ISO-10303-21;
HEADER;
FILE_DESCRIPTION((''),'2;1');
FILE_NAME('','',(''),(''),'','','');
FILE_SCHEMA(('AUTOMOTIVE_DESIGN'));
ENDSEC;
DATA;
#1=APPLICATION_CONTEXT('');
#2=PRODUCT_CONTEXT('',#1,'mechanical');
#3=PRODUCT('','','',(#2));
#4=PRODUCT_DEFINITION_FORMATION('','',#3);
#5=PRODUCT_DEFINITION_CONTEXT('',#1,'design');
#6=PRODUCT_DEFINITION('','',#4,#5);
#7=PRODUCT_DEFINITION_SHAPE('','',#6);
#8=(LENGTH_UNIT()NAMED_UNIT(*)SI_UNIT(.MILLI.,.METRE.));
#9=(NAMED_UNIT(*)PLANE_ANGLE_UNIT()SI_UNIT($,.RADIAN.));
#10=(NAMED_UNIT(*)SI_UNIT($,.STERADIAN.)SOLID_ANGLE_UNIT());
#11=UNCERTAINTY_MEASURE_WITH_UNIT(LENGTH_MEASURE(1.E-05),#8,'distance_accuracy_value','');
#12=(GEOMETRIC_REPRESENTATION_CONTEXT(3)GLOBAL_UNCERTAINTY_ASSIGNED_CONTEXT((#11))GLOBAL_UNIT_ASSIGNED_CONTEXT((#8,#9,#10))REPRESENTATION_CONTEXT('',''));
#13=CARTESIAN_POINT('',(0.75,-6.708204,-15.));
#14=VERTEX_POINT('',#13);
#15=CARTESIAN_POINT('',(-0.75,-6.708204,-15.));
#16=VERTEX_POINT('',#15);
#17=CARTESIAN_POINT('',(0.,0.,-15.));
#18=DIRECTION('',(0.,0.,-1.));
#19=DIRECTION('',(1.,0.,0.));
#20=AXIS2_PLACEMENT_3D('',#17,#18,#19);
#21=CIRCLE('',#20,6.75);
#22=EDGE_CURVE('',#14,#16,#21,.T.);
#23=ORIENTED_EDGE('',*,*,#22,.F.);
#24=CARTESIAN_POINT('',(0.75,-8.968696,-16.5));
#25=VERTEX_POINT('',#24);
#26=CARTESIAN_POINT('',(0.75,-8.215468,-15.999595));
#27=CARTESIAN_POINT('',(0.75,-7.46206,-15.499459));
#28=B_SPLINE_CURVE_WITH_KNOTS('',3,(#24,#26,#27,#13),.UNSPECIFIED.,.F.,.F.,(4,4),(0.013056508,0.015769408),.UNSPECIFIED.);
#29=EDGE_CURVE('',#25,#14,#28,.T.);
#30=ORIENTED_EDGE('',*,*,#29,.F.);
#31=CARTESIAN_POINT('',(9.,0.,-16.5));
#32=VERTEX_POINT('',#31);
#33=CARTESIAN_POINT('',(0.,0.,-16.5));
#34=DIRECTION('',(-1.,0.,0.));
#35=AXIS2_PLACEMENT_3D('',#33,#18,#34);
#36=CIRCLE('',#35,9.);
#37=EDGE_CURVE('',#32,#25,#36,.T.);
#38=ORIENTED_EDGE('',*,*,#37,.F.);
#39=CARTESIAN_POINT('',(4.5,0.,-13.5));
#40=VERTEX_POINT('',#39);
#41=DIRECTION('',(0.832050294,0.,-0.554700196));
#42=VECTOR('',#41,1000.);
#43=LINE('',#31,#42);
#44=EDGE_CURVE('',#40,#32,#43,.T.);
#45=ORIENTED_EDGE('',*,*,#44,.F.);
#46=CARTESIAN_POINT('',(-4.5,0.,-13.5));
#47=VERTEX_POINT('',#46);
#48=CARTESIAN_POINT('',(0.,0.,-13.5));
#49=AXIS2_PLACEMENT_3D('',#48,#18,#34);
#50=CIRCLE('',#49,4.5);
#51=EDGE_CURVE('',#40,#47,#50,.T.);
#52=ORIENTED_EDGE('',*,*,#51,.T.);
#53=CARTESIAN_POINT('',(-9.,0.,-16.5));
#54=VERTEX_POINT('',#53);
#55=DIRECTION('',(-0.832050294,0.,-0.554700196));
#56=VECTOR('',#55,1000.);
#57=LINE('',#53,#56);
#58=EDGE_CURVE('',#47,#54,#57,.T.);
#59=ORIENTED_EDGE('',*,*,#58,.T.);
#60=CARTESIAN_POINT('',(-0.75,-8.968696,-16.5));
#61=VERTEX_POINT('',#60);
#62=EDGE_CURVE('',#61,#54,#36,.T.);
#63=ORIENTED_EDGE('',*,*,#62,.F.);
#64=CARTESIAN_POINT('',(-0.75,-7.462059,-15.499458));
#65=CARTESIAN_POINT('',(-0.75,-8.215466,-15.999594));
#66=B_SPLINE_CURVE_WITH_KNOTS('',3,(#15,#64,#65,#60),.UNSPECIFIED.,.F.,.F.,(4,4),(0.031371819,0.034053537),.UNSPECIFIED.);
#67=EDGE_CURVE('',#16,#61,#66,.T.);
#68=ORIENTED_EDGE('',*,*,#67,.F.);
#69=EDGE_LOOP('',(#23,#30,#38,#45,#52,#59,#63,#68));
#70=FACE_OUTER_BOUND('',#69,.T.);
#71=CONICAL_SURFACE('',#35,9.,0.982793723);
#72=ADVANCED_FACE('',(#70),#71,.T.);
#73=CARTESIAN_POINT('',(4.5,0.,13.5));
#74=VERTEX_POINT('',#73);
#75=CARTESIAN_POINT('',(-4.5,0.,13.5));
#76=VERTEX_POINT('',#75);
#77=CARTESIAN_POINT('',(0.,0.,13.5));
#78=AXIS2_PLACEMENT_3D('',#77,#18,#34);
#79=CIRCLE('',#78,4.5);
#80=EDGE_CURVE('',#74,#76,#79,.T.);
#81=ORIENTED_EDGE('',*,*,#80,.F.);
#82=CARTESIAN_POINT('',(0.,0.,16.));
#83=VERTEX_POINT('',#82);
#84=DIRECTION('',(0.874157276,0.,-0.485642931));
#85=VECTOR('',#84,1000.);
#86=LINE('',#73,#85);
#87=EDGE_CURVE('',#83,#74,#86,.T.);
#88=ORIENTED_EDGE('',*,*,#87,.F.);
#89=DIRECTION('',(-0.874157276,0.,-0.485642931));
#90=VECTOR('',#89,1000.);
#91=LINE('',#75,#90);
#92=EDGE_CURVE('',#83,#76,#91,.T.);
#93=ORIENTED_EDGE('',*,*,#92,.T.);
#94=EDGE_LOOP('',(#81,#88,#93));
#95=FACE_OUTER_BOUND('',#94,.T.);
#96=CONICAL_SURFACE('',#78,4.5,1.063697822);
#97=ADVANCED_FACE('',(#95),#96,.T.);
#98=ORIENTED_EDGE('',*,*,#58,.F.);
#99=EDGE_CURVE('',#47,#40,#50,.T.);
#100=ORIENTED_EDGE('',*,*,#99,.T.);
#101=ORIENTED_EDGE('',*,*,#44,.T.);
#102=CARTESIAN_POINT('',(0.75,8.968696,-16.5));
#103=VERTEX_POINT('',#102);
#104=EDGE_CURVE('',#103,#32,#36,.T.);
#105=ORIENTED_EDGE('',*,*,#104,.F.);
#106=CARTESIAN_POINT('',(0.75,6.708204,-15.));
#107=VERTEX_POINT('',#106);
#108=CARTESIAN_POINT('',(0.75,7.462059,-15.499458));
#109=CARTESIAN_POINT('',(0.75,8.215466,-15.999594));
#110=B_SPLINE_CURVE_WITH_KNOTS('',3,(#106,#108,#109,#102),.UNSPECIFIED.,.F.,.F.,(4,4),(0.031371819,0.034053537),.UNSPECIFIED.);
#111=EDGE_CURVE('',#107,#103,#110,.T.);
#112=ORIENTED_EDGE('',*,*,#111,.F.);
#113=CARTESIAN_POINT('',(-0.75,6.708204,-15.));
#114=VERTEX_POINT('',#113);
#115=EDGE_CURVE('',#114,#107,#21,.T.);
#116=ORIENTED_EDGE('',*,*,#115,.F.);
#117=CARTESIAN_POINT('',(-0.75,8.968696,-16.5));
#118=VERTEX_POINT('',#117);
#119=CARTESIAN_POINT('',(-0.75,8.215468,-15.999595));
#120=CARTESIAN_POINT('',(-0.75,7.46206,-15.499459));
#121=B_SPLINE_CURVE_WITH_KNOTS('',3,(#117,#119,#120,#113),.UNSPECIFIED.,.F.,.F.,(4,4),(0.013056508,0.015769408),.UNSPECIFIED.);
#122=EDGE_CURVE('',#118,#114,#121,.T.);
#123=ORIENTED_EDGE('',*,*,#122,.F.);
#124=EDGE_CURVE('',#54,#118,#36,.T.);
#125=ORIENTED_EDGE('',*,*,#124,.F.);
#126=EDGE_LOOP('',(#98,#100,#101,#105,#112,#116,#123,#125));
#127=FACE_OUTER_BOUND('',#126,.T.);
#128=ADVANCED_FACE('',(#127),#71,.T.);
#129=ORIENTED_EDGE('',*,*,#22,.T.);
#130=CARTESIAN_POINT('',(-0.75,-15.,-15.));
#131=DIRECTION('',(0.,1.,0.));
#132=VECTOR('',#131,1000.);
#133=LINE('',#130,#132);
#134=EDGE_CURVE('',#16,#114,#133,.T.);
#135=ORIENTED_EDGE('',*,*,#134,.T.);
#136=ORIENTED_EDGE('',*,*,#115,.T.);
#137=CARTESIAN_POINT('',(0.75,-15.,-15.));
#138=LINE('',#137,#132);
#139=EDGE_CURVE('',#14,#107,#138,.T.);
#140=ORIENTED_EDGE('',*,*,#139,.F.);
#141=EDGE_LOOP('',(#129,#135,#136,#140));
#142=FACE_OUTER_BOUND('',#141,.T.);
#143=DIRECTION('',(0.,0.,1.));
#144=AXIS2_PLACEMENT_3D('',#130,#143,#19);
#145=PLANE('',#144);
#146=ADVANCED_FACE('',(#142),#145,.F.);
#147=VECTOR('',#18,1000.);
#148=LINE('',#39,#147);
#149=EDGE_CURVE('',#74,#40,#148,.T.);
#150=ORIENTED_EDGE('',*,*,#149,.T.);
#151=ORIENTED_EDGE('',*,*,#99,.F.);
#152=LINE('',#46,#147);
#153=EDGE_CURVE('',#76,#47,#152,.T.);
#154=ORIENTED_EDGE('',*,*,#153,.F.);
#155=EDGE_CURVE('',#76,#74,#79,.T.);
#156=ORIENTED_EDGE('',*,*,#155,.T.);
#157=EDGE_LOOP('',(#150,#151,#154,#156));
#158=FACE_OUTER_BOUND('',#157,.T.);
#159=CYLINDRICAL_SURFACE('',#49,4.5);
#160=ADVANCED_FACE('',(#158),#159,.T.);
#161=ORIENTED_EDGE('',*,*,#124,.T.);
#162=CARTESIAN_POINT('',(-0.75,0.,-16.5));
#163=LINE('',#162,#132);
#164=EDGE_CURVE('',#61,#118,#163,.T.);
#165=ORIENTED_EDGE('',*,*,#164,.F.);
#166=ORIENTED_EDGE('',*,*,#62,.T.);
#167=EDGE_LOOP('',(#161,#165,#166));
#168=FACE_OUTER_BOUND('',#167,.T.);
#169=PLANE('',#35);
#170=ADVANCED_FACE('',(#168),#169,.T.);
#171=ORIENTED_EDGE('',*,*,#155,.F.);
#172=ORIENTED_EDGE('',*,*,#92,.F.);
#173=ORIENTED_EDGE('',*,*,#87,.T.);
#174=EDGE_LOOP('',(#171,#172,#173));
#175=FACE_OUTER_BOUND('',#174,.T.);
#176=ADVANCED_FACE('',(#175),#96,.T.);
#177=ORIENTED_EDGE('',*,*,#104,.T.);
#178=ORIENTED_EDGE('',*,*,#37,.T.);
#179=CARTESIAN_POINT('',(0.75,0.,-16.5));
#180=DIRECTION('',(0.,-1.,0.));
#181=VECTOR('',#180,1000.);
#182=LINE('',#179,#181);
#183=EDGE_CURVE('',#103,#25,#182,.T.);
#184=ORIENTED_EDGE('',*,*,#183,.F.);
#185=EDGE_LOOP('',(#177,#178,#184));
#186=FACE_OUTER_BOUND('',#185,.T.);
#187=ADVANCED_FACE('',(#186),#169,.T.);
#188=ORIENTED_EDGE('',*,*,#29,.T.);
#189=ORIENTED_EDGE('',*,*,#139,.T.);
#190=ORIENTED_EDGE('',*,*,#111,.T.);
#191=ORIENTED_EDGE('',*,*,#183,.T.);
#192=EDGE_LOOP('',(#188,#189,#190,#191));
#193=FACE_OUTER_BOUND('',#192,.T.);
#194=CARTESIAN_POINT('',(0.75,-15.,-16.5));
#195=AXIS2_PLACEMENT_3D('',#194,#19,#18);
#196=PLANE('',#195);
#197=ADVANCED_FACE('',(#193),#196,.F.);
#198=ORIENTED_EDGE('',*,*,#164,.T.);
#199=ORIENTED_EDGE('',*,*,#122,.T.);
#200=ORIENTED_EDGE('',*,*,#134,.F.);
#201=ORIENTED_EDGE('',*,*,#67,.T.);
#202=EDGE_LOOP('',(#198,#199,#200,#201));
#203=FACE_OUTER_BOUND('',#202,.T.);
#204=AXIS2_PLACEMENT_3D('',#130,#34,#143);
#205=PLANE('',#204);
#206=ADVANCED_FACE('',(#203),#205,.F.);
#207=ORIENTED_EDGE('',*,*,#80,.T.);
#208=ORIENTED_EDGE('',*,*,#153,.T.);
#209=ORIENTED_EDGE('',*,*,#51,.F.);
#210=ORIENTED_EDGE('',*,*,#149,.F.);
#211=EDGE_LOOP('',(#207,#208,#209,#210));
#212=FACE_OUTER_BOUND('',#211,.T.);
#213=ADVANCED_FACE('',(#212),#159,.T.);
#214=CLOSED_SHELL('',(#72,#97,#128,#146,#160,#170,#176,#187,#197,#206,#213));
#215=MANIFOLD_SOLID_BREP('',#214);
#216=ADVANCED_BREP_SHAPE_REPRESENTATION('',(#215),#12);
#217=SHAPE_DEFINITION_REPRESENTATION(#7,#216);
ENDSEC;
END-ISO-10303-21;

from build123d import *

# Parameters (mm, degrees)
SKETCH1_W          = 4.5
SKETCH1_H          = 27
CUT_EXTRUDE1_DEPTH = 15


with BuildPart() as part:
    # Sketch1 → Revolve3 (revolve)
    with BuildSketch(Plane(origin=(0, 0, 0), x_dir=(1, 0, 0), z_dir=(0, 1, 0)), mode=Mode.PRIVATE) as revolve3_sk:
        with Locations((2.25, 0)):
            Rectangle(SKETCH1_W, SKETCH1_H)
        Polygon((0, -13.5), (4.5, -13.5), (0, -16), align=None)
        Polygon((9, 16.5), (4.5, 13.5), (0, 13.5), (0, 16.5), align=None)
    revolve(revolve3_sk.sketch.rotate(Axis((0, 0, -13.5), (0, 0, 1)), 180), axis=Axis((0, 0, -13.5), (0, 0, 1)))

    # Sketch2 → Cut-Extrude1 (cut, symmetric)
    with BuildSketch(Plane(origin=(0, 0, 0), x_dir=(1, 0, 0), z_dir=(0, 1, 0))):
        Polygon((0, 16.5), (0.75, 16.5), (0.75, 15), (-0.75, 15), (-0.75, 16.5), align=None)
    extrude(amount=CUT_EXTRUDE1_DEPTH, both=True, mode=Mode.SUBTRACT)


solid = part.part
